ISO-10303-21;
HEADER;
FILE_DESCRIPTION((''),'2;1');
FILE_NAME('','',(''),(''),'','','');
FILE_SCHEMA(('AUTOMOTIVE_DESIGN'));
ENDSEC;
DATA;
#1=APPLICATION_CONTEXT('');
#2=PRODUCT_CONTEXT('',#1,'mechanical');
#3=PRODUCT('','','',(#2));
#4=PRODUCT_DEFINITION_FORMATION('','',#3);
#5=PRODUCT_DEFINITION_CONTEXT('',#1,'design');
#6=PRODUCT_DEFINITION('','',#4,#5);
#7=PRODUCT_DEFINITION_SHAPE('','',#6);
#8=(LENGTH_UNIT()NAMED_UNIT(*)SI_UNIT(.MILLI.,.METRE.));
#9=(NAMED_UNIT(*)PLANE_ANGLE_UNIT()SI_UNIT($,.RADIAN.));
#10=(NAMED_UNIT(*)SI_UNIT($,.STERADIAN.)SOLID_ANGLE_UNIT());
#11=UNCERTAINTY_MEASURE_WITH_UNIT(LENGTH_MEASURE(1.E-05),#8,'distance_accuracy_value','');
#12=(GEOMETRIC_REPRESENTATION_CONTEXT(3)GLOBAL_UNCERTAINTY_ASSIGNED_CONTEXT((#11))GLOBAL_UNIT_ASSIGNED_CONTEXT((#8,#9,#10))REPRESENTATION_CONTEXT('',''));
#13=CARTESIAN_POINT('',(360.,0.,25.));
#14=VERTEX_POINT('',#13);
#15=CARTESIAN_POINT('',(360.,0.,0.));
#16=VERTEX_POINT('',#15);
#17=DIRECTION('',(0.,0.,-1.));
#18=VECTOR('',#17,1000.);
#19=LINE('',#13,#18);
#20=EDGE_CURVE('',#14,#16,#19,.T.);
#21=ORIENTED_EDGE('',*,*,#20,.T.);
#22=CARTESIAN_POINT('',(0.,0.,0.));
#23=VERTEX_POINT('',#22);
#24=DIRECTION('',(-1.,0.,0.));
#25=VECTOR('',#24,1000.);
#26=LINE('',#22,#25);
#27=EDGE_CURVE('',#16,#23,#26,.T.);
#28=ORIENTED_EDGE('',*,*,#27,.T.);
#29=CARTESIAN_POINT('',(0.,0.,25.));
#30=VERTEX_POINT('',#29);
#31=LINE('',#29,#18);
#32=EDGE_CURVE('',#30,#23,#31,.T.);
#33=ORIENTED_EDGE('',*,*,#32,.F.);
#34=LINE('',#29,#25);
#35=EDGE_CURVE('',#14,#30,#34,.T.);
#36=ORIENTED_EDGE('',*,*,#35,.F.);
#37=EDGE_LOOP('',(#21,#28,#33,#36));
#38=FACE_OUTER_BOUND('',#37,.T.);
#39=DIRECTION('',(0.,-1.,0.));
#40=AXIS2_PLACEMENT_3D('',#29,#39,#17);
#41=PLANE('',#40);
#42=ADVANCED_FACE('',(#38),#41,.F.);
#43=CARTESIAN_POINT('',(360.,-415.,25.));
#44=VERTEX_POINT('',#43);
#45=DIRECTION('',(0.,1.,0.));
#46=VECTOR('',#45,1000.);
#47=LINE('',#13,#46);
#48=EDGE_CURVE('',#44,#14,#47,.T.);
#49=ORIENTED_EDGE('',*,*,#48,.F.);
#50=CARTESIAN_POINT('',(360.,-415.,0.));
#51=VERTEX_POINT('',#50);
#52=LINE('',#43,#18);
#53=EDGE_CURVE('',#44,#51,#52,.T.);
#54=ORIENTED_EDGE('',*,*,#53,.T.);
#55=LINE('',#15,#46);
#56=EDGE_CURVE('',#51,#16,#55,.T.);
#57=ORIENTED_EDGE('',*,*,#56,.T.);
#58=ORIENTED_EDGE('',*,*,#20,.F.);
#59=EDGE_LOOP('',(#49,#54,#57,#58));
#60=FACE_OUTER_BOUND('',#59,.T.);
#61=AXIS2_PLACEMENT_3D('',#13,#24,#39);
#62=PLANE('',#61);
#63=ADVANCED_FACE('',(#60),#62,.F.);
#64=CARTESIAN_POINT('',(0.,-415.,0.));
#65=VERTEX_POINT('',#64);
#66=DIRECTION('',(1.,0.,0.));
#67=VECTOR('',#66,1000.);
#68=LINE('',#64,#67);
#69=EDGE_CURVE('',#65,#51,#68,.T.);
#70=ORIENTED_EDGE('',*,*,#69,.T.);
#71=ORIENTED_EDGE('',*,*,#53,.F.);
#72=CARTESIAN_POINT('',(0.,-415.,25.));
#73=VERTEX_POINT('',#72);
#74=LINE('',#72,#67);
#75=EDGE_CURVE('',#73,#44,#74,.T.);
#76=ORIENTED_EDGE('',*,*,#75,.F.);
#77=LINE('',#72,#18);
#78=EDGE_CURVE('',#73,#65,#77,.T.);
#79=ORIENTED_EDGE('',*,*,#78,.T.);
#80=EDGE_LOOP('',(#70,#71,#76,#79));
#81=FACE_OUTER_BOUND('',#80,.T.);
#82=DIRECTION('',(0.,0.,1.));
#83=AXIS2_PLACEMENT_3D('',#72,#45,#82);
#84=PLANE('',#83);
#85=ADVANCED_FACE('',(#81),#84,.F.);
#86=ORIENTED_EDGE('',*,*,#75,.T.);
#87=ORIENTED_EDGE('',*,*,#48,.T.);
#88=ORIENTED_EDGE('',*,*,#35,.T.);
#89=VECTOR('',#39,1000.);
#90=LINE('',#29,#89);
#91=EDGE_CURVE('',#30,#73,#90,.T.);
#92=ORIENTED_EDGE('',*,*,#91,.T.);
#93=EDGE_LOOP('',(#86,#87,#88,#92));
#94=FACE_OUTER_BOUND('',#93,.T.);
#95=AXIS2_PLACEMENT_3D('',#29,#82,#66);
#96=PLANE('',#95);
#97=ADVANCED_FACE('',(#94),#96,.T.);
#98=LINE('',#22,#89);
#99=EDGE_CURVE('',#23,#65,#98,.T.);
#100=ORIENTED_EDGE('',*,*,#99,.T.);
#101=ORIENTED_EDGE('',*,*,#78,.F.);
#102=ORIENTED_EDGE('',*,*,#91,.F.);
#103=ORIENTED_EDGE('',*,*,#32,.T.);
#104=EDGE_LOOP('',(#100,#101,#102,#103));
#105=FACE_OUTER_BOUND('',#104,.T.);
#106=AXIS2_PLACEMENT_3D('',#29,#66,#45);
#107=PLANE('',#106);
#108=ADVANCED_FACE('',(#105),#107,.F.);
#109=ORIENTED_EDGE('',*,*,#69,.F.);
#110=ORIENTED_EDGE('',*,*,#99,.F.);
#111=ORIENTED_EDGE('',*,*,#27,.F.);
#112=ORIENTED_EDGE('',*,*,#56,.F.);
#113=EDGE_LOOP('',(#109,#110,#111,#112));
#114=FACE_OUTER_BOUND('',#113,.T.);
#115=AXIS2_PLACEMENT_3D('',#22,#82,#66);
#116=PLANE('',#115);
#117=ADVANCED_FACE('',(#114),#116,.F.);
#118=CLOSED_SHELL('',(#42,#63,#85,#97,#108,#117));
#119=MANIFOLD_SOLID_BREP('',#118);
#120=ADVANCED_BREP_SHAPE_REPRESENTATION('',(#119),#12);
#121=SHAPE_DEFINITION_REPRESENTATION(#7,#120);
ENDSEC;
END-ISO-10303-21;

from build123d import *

# Parameters (mm, degrees)
SKETCH1_W           = 360
SKETCH1_H           = 415
BOSS_EXTRUDE1_DEPTH = 25


with BuildPart() as part:
    # Sketch1 → Boss-Extrude1 (new body)
    with BuildSketch(Plane.XY):
        with Locations((180, -207.5)):
            Rectangle(SKETCH1_W, SKETCH1_H)
    extrude(amount=BOSS_EXTRUDE1_DEPTH)


solid = part.part
